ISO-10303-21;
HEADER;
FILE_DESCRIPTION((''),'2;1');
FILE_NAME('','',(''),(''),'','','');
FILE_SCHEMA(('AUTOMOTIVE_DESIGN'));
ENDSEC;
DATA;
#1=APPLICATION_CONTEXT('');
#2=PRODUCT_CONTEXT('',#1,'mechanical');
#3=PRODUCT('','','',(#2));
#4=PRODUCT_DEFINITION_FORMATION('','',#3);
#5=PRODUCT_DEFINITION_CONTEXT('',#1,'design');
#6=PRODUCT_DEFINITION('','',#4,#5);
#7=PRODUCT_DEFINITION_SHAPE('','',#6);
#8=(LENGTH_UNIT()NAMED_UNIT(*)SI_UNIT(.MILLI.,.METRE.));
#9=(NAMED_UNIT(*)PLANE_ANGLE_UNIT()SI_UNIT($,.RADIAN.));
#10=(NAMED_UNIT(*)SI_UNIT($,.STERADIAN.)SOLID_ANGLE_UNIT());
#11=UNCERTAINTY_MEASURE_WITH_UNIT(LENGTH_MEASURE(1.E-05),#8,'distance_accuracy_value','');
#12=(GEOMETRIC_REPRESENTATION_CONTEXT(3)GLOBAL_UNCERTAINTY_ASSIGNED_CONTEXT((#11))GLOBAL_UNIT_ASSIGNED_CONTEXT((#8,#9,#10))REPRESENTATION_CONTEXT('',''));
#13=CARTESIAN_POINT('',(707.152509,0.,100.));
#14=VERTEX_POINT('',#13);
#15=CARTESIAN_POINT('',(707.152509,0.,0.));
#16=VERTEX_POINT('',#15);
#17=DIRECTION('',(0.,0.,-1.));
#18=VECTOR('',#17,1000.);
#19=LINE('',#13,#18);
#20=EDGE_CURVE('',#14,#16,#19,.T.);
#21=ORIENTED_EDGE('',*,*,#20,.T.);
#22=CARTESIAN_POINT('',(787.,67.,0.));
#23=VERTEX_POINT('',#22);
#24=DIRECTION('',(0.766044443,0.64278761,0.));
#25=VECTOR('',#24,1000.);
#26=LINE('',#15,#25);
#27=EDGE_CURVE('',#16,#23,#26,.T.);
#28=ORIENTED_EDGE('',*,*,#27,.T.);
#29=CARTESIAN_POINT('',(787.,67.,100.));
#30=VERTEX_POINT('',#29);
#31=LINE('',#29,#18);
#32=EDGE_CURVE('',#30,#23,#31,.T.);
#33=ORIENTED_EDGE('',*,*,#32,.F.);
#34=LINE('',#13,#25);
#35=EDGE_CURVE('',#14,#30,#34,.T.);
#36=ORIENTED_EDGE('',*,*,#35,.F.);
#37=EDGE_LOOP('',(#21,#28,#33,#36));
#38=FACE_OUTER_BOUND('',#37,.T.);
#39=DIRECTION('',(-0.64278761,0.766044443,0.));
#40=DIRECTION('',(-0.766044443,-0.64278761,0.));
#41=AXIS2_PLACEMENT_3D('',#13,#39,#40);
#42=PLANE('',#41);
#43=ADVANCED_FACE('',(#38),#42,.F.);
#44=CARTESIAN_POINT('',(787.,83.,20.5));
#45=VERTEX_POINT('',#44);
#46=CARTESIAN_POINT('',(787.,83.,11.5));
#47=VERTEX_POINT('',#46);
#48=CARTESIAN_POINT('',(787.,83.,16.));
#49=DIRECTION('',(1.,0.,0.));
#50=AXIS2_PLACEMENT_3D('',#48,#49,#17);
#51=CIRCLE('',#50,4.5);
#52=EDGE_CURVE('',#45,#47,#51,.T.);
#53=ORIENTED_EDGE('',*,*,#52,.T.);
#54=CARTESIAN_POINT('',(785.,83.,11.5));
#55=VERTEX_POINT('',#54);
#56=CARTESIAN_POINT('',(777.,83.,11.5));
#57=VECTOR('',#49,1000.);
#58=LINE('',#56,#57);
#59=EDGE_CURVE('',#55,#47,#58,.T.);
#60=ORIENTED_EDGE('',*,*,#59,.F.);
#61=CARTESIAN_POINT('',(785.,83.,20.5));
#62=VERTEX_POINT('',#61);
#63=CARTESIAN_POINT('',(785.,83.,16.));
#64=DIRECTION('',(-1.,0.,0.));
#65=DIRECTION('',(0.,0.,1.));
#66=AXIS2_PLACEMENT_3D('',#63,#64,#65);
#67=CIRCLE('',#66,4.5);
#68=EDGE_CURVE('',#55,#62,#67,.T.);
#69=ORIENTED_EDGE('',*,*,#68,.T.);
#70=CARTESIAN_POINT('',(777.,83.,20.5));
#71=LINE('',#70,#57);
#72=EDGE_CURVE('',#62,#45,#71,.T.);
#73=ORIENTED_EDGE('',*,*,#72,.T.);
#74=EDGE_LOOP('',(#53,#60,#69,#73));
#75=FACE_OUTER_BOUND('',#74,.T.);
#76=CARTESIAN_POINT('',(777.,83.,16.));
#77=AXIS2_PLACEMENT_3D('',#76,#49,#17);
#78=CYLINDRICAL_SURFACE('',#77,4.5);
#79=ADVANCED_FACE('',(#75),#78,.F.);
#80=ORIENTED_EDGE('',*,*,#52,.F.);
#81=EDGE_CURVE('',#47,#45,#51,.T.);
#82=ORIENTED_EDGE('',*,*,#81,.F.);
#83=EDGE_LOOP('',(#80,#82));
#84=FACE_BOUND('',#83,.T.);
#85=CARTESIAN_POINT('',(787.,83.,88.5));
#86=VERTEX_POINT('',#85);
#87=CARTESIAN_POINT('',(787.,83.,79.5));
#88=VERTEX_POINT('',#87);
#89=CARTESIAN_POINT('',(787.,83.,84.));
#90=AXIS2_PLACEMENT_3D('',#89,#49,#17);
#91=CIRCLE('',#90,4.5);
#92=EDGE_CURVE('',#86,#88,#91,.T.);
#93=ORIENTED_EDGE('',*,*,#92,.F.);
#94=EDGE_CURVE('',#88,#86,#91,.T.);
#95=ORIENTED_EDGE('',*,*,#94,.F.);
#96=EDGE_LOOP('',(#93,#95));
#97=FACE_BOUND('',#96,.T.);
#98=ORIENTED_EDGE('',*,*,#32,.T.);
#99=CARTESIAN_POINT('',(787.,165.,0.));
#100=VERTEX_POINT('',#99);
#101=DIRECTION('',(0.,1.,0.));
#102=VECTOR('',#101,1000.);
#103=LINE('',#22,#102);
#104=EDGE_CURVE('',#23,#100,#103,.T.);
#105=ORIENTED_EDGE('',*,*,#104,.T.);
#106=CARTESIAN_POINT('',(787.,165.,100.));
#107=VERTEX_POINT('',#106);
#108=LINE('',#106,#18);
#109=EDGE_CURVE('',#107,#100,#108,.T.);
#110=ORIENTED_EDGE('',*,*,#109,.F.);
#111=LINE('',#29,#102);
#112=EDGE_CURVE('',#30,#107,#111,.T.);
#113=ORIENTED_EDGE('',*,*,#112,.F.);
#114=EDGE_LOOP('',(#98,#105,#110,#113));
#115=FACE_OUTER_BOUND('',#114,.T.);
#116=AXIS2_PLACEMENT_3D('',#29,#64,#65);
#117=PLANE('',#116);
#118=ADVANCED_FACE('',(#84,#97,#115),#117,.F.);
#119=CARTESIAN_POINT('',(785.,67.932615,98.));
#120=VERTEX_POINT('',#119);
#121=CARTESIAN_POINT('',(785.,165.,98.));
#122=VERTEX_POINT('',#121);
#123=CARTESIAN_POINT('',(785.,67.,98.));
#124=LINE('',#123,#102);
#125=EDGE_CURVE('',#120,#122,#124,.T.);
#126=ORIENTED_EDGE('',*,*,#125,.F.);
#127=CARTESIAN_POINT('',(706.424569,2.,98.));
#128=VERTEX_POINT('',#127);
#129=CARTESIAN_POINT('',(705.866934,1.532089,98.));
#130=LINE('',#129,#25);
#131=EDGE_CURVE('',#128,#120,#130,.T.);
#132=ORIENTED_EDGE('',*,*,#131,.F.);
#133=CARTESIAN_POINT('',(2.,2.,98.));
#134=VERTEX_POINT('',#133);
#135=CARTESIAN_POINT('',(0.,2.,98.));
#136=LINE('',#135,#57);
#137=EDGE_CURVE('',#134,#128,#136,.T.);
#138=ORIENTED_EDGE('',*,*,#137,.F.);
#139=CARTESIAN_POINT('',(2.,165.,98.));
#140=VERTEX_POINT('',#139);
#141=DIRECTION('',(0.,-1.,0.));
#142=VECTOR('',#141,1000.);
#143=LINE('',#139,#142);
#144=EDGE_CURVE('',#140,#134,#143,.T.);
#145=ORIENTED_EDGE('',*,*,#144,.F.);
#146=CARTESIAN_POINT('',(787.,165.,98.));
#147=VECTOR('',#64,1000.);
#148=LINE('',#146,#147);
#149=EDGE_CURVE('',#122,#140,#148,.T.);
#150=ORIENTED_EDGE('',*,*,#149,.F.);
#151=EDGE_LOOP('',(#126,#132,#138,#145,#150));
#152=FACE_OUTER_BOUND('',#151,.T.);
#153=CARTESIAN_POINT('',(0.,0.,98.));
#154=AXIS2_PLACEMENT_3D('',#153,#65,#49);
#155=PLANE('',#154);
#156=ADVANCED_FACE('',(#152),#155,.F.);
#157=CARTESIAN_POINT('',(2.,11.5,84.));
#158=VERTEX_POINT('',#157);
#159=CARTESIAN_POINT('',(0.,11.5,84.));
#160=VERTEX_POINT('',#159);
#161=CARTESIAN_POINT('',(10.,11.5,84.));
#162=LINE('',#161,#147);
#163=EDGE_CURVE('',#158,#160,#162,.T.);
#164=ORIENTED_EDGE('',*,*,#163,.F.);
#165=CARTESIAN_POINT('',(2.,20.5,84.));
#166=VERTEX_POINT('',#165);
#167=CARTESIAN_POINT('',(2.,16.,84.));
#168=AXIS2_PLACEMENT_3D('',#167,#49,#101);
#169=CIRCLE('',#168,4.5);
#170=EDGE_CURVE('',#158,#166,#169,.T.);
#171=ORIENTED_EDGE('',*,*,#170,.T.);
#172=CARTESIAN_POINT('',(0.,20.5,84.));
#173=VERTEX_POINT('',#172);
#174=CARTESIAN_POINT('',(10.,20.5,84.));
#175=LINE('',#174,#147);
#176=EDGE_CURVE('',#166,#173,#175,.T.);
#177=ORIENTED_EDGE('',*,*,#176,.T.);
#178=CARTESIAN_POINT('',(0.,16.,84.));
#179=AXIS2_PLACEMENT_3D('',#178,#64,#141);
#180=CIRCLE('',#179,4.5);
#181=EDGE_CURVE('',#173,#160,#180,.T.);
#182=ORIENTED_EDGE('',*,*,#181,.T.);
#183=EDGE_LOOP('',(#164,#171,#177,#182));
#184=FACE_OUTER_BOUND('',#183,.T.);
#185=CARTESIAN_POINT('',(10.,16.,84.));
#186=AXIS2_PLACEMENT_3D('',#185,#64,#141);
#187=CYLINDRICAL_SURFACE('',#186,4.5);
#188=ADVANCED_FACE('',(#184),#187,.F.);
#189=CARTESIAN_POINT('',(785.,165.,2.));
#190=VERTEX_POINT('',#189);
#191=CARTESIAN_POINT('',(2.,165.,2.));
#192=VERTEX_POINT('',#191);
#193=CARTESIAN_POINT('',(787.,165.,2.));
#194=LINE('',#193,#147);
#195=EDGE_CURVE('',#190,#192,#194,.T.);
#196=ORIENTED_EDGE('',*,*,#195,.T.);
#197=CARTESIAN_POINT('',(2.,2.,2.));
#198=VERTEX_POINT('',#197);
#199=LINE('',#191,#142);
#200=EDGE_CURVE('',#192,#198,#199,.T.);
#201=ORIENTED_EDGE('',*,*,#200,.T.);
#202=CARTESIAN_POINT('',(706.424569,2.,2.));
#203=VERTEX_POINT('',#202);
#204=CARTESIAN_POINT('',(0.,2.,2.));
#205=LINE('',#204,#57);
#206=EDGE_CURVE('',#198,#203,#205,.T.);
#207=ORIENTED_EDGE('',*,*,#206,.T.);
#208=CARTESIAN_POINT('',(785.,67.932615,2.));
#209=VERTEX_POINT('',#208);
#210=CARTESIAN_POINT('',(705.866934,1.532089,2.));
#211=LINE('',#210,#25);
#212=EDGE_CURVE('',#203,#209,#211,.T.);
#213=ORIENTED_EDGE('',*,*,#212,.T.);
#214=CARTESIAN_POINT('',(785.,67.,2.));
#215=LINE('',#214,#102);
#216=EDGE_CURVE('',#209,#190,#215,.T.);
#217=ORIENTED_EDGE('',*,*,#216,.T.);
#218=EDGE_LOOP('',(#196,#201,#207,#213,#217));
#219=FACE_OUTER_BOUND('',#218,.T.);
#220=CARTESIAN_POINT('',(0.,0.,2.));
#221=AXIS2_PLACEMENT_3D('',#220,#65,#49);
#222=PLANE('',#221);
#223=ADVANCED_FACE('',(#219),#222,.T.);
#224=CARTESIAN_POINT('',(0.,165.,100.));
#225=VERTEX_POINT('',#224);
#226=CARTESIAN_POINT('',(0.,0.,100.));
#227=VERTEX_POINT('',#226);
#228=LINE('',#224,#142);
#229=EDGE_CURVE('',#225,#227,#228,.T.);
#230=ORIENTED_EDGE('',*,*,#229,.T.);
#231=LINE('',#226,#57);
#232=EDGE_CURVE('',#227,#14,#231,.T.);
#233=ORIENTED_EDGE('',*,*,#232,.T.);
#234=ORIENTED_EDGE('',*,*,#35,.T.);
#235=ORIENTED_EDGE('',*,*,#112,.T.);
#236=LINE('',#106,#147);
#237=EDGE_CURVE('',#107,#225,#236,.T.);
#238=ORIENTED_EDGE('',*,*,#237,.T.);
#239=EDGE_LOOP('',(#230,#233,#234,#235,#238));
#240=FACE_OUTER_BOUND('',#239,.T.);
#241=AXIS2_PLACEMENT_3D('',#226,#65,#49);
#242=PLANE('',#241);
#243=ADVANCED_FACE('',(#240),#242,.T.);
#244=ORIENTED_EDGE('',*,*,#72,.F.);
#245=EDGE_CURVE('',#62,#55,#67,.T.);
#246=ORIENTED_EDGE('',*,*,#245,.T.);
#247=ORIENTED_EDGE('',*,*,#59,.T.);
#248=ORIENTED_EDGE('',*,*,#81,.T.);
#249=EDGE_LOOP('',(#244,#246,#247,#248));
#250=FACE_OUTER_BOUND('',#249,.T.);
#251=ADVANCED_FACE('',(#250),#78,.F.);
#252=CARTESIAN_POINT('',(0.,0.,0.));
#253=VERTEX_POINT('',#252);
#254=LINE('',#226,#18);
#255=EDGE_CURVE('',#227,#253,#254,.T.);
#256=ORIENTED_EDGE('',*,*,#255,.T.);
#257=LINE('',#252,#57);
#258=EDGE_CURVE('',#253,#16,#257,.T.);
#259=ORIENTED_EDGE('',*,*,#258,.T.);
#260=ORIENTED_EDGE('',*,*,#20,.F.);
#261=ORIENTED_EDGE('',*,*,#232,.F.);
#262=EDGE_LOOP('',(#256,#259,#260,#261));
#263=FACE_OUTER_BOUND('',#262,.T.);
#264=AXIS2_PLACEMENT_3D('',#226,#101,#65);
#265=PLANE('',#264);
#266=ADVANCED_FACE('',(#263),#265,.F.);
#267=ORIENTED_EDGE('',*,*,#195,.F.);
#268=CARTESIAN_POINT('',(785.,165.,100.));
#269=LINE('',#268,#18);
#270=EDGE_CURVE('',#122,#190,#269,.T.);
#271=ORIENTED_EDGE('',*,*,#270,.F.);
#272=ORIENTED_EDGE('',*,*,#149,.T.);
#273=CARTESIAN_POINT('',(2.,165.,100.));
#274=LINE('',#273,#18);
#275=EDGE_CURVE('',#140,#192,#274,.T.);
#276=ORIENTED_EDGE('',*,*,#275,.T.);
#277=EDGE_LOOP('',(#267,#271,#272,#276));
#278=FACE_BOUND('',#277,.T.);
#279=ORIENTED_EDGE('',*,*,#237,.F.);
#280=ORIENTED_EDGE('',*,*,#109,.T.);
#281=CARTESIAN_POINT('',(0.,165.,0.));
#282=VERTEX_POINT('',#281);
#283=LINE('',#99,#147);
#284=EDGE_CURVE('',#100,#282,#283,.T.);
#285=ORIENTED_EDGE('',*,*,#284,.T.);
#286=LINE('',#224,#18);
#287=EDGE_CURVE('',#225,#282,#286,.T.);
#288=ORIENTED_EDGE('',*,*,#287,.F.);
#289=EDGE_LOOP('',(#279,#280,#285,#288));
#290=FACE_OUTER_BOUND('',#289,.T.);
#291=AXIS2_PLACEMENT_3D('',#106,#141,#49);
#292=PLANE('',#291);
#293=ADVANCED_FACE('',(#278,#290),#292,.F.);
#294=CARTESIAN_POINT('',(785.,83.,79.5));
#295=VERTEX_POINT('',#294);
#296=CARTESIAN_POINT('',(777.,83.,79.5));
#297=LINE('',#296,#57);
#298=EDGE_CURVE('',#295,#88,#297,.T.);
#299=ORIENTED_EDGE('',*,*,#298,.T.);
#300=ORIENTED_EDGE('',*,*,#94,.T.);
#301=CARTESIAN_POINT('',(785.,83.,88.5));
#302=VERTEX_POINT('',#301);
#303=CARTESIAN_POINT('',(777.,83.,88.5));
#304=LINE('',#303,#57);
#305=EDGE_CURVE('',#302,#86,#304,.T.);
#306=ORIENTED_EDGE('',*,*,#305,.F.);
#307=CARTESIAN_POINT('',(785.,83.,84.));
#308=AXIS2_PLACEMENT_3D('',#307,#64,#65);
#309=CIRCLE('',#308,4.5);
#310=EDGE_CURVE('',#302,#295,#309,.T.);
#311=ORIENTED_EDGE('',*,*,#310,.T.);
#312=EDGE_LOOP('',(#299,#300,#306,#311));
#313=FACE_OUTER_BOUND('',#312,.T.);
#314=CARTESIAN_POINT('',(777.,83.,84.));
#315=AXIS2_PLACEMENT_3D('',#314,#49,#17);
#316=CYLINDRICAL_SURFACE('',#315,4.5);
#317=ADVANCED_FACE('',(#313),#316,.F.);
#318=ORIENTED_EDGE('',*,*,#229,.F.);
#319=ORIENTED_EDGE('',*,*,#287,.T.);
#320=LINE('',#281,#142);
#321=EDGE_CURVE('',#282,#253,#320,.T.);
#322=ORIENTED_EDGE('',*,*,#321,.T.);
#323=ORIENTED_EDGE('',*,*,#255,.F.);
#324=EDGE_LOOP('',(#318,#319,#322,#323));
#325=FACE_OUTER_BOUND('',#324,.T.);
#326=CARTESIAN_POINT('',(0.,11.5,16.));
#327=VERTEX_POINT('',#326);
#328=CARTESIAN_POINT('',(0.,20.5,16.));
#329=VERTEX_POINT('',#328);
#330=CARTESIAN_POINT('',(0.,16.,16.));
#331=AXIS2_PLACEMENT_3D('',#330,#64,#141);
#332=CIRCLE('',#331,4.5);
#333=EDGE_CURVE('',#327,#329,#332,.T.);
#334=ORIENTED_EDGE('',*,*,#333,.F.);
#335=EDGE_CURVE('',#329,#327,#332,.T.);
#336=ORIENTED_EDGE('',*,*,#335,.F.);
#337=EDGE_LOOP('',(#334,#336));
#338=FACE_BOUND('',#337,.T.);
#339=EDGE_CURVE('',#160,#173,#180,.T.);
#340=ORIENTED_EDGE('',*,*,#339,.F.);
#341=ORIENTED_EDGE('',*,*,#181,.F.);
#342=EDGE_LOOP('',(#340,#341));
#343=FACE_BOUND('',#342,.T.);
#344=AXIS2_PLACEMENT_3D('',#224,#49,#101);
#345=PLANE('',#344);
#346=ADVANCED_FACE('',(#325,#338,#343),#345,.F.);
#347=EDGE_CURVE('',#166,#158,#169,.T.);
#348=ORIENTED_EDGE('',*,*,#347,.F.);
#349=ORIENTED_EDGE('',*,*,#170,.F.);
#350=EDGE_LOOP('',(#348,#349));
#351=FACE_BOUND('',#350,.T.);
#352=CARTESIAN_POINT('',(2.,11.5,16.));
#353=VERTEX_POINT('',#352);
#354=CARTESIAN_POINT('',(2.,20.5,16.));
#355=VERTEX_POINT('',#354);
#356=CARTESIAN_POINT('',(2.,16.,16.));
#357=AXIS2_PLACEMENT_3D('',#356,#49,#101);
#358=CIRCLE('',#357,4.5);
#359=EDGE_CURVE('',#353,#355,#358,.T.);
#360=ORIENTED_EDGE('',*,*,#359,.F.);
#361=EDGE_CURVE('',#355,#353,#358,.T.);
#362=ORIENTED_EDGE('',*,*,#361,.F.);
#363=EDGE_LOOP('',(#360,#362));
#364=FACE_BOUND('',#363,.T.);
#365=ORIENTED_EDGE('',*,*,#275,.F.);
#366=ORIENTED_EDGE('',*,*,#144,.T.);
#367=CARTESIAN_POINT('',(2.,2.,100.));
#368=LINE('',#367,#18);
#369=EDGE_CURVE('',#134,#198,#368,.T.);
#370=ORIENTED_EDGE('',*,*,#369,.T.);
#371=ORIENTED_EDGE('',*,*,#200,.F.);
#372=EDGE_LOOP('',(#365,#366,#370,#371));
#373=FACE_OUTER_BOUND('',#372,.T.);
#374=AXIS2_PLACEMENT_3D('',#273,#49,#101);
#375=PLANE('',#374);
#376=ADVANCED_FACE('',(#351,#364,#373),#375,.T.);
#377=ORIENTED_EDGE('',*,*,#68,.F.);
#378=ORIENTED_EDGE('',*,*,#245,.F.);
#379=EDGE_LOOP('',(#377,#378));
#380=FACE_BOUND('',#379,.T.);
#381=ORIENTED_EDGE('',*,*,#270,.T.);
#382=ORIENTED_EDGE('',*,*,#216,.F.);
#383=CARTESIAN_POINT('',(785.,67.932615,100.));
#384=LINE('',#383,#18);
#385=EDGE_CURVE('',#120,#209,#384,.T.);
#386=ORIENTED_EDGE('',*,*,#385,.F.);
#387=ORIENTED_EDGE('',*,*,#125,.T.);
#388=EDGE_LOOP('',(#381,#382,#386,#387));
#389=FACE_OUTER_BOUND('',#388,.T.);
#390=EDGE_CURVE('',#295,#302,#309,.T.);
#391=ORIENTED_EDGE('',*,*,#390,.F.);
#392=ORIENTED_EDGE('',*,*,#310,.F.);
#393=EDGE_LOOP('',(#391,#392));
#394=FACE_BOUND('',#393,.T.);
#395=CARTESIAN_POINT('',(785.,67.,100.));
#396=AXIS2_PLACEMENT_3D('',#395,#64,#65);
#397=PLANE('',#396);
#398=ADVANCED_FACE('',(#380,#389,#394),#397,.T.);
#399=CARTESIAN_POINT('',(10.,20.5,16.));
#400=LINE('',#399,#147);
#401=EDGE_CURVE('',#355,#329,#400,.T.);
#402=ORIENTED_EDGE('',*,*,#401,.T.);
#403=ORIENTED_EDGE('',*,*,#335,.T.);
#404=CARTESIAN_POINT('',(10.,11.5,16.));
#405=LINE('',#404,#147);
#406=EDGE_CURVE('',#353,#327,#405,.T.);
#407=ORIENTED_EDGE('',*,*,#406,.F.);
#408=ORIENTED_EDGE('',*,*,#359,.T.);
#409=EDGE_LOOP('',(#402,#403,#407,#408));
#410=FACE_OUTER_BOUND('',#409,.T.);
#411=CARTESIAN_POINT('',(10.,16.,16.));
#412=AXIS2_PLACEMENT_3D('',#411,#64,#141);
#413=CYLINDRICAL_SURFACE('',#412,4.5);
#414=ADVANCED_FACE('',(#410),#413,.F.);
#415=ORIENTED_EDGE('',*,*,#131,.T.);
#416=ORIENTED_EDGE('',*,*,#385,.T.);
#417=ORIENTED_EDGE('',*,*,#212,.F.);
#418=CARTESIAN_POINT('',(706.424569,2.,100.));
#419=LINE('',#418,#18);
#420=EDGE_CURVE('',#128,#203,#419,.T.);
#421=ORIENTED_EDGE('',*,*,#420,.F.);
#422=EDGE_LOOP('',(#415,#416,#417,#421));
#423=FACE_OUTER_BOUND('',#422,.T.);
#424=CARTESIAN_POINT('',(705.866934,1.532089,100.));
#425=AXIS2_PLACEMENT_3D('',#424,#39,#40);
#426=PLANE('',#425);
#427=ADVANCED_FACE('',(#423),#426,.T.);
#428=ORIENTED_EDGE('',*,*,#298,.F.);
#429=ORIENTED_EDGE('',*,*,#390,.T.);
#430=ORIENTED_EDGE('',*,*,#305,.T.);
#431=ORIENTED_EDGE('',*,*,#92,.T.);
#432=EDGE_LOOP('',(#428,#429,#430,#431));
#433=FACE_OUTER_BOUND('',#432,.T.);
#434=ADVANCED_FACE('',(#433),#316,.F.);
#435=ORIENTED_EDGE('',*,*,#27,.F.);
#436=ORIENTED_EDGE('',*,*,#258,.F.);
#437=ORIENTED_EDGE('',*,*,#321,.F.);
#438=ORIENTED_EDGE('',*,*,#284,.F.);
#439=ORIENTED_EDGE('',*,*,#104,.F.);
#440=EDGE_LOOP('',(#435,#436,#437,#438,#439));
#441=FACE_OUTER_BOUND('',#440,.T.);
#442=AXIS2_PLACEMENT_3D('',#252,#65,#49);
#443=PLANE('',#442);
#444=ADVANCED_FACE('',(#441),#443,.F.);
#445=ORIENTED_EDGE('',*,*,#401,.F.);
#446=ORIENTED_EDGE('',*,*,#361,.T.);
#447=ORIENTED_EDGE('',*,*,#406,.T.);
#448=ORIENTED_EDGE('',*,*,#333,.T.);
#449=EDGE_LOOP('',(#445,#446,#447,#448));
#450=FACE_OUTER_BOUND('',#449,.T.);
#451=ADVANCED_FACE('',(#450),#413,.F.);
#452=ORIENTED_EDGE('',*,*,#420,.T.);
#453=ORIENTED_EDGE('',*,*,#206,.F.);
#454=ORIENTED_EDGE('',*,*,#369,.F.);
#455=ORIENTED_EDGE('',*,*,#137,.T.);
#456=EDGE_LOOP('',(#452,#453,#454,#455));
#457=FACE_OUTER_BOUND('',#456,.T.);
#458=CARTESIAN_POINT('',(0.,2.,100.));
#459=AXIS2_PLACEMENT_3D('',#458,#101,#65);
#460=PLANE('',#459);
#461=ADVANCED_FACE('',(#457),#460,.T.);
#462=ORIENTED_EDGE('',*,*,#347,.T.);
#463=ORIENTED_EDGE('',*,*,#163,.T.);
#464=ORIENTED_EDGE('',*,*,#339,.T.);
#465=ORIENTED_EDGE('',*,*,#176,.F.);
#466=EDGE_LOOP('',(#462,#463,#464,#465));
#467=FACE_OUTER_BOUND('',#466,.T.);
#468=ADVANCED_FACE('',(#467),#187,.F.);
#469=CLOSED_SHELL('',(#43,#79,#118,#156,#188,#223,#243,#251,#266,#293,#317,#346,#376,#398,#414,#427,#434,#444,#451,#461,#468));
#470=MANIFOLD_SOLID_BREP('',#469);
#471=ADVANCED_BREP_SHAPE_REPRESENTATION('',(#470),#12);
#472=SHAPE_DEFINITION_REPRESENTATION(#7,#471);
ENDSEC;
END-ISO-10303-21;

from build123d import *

# Parameters (mm, degrees)
EXTRUDE_1_DEPTH     = 100
SHELL_1_T           = -2
SKETCH_2_R          = 4.5
CUT_EXTRUDE_1_DEPTH = 10
SKETCH_3_R          = 4.5
CUT_EXTRUDE_2_DEPTH = 10


with BuildPart() as part:
    # 草图1 → 凸台-拉伸1 (new body)
    with BuildSketch(Plane.XY):
        Polygon((0, 0), (707.152509296, 0), (787, 67), (787, 165), (0, 165), align=None)
    extrude(amount=EXTRUDE_1_DEPTH)

    # 抽壳1
    shell_1_openings = [part.faces().sort_by_distance(p)[0] for p in [
        (393.5, 165, 50),
    ]]
    offset(amount=SHELL_1_T, openings=shell_1_openings, kind=Kind.INTERSECTION)

    # 草图2 → 切除-拉伸1 (cut)
    with BuildSketch(Plane.ZY):
        with Locations(Location((16, 16, 0), (0, 0, 270))):
            Circle(SKETCH_2_R)
        with Locations(Location((84, 16, 0), (0, 0, 270))):
            Circle(SKETCH_2_R)
    extrude(amount=-CUT_EXTRUDE_1_DEPTH, mode=Mode.SUBTRACT)

    # 草图3 → 切除-拉伸2 (cut)
    with BuildSketch(Plane(origin=(787, 0, 0), x_dir=(0, 0, -1), z_dir=(1, 0, 0))):
        with Locations((-84, 83)):
            Circle(SKETCH_3_R)
        with Locations((-16, 83)):
            Circle(SKETCH_3_R)
    extrude(amount=-CUT_EXTRUDE_2_DEPTH, mode=Mode.SUBTRACT)


solid = part.part
